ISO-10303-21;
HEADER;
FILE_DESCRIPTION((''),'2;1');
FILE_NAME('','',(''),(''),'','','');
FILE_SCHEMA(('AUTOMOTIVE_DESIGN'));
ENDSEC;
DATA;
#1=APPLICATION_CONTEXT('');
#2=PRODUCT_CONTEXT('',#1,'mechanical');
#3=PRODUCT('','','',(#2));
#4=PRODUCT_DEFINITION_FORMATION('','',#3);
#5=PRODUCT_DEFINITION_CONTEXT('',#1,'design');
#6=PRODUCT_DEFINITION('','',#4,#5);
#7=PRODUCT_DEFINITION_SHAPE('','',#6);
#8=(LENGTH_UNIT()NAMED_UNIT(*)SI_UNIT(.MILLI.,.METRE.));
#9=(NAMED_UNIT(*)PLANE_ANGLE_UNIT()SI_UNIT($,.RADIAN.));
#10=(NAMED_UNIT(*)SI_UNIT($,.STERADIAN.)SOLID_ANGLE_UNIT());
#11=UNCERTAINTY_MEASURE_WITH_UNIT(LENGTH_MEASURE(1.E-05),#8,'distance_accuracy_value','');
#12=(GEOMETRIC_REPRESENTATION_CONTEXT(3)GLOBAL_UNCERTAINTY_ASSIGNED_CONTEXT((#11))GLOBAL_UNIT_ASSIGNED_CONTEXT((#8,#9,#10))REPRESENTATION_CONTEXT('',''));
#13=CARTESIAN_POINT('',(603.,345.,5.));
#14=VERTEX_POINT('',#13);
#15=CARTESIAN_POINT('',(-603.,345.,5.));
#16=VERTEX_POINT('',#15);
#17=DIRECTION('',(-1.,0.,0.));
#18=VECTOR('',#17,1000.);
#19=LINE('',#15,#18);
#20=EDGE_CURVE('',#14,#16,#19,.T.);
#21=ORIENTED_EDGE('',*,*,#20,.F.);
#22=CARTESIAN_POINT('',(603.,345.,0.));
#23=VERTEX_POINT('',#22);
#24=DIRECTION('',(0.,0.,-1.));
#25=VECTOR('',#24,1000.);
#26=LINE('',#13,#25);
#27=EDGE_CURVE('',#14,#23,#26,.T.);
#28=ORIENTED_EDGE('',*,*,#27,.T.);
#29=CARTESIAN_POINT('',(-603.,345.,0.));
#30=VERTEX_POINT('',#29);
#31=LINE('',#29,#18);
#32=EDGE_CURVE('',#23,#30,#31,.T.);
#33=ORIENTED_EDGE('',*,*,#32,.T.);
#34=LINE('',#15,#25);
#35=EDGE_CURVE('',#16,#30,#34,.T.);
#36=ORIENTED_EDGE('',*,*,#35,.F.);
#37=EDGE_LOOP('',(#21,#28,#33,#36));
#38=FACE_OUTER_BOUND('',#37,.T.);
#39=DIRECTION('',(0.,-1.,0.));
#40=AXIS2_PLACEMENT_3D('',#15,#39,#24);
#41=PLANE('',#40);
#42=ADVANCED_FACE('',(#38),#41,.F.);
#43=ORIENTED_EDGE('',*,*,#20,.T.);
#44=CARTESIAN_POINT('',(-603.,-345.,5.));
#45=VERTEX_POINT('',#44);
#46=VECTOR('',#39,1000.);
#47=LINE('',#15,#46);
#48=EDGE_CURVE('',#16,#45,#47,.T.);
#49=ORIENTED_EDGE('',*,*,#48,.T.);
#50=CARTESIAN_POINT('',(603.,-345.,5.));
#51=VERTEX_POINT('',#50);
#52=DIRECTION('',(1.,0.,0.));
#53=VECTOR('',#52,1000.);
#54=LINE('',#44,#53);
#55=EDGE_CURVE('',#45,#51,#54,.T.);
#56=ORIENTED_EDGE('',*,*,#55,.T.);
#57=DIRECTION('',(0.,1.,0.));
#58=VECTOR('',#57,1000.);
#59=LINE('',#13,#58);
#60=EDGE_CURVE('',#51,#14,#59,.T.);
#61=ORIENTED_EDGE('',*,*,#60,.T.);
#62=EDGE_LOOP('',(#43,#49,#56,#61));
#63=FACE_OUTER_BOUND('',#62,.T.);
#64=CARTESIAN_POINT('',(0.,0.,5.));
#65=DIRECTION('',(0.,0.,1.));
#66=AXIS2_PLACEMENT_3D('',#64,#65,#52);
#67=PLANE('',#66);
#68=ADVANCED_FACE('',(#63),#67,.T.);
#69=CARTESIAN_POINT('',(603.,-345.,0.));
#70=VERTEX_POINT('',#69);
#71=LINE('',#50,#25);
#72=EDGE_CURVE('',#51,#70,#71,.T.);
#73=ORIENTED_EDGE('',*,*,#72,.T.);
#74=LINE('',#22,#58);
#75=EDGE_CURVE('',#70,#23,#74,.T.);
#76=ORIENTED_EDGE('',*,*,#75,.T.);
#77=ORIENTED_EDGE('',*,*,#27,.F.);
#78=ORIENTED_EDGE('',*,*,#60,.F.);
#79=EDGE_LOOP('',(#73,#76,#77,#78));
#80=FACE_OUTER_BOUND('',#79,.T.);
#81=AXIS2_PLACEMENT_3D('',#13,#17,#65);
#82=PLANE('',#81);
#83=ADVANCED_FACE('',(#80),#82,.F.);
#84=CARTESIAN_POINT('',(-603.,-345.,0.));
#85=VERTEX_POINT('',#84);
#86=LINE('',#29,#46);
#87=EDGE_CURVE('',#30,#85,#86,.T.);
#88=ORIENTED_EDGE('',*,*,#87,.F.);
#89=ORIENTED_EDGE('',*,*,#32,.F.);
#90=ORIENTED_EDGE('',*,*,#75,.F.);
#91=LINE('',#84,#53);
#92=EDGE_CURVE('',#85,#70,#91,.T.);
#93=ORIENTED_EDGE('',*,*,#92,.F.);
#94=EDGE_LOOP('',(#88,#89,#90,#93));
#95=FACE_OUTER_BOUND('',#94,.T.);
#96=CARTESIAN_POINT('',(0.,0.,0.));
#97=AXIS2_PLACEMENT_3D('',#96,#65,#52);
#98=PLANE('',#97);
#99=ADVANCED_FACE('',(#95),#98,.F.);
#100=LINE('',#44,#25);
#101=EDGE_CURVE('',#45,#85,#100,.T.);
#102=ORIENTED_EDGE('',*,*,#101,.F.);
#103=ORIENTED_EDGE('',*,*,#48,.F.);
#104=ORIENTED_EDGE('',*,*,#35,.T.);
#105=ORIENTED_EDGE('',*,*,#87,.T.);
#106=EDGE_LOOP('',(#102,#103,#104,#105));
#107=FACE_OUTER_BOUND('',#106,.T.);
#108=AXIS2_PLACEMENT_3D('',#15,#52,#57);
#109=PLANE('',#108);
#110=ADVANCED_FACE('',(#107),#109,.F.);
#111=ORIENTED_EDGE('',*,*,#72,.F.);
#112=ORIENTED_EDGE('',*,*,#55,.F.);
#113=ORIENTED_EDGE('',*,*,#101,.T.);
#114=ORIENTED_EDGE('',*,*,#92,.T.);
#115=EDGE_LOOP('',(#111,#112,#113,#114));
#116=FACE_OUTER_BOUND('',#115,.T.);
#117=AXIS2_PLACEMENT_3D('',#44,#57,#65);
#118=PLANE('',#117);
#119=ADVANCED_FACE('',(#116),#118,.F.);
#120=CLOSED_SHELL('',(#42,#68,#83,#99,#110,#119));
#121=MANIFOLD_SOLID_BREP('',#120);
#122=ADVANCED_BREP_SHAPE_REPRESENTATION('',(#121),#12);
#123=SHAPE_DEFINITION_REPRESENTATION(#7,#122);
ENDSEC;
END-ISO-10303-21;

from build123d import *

# Parameters (mm, degrees)
SKETCH_1_W      = 1206
SKETCH_1_H      = 690
EXTRUDE_1_DEPTH = 5


with BuildPart() as part:
    # 草图1 → 凸台-拉伸1 (new body)
    with BuildSketch(Plane.XY):
        Rectangle(SKETCH_1_W, SKETCH_1_H)
    extrude(amount=EXTRUDE_1_DEPTH)


solid = part.part
